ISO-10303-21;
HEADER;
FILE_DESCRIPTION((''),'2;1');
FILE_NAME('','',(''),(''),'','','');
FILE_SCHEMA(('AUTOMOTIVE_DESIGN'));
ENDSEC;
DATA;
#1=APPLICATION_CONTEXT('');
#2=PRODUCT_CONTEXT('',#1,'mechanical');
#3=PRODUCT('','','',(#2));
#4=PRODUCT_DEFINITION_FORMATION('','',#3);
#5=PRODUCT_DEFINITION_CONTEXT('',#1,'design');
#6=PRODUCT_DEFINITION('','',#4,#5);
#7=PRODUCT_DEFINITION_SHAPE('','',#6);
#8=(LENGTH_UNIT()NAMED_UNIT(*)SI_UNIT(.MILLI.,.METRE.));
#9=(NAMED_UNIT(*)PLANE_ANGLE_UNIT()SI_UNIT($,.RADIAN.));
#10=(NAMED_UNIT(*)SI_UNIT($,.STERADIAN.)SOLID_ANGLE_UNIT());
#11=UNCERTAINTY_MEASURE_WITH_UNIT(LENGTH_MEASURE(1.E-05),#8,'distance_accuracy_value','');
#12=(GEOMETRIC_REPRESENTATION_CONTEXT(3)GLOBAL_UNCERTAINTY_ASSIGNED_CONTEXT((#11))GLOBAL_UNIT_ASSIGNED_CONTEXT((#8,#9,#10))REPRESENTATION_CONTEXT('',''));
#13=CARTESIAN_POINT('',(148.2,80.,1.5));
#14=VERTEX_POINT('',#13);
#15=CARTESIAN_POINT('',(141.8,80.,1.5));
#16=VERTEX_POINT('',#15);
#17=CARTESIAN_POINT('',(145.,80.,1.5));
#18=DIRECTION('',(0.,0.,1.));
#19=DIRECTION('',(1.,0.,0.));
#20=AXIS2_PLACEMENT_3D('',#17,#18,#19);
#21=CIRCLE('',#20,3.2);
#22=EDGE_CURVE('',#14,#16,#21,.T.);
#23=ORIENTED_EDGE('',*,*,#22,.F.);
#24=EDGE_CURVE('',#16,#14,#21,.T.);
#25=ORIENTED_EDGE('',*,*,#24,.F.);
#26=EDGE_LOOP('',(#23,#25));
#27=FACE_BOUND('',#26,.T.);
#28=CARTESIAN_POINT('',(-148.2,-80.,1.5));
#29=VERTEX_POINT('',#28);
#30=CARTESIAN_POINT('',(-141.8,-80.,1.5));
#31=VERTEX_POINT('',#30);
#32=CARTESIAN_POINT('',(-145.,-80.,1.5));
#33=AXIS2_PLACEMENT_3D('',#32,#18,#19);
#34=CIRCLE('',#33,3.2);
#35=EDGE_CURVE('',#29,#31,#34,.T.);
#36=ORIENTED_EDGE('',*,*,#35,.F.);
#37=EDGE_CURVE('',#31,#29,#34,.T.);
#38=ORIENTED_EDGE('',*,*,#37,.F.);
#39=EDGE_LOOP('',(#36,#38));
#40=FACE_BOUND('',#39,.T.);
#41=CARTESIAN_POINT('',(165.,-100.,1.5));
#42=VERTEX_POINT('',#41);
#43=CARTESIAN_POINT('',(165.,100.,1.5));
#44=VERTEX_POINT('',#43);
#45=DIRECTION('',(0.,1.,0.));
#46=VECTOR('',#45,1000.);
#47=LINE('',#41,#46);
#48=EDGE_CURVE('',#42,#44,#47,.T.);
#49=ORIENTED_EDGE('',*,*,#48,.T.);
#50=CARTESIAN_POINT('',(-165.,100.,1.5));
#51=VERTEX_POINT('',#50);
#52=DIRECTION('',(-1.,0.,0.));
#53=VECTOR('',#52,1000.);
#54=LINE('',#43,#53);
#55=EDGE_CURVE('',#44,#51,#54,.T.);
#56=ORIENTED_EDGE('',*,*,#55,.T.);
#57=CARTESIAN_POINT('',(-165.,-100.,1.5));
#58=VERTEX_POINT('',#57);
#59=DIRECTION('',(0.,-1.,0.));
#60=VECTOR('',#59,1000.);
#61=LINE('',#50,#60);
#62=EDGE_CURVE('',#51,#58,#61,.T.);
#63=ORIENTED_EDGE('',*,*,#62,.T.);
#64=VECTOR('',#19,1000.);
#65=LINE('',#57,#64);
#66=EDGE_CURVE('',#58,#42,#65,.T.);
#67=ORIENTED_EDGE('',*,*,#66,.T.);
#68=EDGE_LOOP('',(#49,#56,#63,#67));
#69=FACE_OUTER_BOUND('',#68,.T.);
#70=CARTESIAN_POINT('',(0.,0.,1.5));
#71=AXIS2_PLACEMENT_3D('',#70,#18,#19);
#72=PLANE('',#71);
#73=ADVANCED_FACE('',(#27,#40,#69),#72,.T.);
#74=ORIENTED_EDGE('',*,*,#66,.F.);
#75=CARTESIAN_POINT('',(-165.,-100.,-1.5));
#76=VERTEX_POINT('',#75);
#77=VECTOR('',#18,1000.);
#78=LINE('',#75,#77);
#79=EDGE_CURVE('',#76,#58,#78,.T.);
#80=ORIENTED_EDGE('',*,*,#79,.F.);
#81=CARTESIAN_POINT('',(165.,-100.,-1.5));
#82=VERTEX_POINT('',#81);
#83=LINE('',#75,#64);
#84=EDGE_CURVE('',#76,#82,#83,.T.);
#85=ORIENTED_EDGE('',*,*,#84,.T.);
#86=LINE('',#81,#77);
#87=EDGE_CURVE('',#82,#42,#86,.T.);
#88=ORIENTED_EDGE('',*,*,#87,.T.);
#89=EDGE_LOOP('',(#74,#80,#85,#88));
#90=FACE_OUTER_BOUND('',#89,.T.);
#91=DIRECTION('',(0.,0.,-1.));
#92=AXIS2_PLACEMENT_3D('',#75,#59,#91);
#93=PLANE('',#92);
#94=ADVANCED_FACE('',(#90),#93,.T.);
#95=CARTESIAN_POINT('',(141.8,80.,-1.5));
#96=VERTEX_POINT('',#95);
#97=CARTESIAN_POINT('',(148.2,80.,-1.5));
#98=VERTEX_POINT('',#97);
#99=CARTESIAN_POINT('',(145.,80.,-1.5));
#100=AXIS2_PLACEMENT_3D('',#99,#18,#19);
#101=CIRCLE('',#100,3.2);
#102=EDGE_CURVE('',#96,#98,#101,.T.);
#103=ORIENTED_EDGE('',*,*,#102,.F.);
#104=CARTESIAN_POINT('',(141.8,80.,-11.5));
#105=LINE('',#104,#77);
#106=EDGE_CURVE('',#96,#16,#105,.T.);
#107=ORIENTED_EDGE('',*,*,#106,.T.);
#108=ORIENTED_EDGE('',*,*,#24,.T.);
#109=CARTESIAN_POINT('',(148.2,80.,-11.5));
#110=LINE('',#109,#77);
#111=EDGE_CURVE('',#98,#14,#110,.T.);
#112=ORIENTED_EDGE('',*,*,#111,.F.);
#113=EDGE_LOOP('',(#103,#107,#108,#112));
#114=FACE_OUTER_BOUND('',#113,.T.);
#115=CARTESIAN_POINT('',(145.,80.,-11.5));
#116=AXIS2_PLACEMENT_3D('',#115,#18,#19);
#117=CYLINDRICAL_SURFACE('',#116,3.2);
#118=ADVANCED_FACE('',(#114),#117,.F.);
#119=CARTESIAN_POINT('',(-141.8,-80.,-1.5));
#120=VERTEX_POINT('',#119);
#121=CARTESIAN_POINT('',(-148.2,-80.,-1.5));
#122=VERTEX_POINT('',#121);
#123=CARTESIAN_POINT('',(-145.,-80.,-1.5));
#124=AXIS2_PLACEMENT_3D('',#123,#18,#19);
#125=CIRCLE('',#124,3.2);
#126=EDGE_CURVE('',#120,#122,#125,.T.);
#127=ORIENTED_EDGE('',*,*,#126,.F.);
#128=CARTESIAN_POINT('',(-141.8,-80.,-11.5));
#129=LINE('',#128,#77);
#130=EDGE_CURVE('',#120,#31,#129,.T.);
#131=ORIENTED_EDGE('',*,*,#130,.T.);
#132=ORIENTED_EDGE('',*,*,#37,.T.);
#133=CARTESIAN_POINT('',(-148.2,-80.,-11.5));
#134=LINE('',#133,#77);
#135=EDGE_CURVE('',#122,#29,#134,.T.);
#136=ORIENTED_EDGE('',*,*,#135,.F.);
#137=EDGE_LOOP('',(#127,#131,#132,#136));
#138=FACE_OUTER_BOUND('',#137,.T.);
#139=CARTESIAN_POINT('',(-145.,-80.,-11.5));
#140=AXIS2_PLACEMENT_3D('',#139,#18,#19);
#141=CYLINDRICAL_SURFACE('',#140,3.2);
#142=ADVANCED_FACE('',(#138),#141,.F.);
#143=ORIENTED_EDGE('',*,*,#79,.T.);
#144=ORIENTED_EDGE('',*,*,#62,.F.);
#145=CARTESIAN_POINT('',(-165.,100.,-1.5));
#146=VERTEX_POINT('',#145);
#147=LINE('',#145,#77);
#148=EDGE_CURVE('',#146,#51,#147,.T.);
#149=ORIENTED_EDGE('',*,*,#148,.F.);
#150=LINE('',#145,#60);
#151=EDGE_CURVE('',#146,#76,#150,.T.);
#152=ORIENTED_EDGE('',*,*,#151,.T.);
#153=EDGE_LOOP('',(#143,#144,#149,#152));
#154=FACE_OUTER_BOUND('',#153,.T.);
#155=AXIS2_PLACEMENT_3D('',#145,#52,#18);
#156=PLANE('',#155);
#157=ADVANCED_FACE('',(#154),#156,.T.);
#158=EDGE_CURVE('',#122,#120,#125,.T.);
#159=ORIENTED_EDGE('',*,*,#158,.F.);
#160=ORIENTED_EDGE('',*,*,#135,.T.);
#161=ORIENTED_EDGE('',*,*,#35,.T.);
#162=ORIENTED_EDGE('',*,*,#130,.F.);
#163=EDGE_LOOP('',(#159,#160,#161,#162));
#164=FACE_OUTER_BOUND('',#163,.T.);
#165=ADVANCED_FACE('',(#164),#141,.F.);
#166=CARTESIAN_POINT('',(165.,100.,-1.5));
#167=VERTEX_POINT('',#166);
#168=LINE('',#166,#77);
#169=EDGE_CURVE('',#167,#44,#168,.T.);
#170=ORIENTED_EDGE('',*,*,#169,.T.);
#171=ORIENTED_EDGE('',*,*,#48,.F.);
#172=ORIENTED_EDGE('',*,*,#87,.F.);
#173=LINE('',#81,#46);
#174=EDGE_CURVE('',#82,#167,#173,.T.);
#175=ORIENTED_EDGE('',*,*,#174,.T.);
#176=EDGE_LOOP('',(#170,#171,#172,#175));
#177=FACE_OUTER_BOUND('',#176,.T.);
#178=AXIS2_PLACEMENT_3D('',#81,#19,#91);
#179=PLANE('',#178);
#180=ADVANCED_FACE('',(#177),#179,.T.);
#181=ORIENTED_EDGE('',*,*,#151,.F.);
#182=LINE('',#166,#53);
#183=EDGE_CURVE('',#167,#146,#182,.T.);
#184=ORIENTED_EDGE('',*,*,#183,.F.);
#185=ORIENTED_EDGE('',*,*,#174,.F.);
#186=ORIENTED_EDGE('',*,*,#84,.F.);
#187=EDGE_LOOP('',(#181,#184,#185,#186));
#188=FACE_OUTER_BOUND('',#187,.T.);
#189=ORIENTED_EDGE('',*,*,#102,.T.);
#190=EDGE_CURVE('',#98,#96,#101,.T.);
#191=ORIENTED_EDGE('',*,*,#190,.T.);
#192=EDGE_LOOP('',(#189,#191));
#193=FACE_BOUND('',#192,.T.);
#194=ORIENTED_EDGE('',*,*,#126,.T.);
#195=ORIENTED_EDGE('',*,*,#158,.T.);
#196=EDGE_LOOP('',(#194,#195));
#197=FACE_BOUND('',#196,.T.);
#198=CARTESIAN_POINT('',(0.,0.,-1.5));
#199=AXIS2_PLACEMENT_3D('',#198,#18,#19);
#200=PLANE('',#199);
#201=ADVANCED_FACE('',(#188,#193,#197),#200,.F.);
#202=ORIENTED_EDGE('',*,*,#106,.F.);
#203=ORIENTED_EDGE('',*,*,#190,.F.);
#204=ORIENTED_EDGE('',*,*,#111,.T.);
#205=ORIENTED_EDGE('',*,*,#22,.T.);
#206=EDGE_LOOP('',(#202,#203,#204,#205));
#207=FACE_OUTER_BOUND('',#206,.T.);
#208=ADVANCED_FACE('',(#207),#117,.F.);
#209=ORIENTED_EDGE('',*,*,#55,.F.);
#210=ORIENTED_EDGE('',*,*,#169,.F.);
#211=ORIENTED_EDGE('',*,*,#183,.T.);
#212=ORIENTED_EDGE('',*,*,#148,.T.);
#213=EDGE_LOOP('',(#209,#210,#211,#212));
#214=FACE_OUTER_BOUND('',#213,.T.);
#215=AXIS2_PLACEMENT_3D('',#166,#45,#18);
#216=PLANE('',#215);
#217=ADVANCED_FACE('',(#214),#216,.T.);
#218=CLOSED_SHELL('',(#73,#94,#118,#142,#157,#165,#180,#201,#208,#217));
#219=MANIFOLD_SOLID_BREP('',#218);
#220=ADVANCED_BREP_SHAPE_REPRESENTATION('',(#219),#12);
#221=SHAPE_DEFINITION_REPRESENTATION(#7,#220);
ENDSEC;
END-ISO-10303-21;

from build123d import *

# Parameters (mm, degrees)
SKETCH_1_W          = 330
SKETCH_1_H          = 200
EXTRUDE_1_DEPTH     = 1.5
SKETCH_2_R          = 3.2
CUT_EXTRUDE_1_DEPTH = 11.5


with BuildPart() as part:
    # 草图1 → 凸台-拉伸1 (new, symmetric)
    with BuildSketch(Plane.XY):
        Rectangle(SKETCH_1_W, SKETCH_1_H)
    extrude(amount=EXTRUDE_1_DEPTH, both=True)

    # 草图2 → 切除-拉伸1 (cut, symmetric)
    with BuildSketch(Plane.XY):
        with Locations((-145, -80)):
            Circle(SKETCH_2_R)
        with Locations((145, 80)):
            Circle(SKETCH_2_R)
    extrude(amount=CUT_EXTRUDE_1_DEPTH, both=True, mode=Mode.SUBTRACT)


solid = part.part
